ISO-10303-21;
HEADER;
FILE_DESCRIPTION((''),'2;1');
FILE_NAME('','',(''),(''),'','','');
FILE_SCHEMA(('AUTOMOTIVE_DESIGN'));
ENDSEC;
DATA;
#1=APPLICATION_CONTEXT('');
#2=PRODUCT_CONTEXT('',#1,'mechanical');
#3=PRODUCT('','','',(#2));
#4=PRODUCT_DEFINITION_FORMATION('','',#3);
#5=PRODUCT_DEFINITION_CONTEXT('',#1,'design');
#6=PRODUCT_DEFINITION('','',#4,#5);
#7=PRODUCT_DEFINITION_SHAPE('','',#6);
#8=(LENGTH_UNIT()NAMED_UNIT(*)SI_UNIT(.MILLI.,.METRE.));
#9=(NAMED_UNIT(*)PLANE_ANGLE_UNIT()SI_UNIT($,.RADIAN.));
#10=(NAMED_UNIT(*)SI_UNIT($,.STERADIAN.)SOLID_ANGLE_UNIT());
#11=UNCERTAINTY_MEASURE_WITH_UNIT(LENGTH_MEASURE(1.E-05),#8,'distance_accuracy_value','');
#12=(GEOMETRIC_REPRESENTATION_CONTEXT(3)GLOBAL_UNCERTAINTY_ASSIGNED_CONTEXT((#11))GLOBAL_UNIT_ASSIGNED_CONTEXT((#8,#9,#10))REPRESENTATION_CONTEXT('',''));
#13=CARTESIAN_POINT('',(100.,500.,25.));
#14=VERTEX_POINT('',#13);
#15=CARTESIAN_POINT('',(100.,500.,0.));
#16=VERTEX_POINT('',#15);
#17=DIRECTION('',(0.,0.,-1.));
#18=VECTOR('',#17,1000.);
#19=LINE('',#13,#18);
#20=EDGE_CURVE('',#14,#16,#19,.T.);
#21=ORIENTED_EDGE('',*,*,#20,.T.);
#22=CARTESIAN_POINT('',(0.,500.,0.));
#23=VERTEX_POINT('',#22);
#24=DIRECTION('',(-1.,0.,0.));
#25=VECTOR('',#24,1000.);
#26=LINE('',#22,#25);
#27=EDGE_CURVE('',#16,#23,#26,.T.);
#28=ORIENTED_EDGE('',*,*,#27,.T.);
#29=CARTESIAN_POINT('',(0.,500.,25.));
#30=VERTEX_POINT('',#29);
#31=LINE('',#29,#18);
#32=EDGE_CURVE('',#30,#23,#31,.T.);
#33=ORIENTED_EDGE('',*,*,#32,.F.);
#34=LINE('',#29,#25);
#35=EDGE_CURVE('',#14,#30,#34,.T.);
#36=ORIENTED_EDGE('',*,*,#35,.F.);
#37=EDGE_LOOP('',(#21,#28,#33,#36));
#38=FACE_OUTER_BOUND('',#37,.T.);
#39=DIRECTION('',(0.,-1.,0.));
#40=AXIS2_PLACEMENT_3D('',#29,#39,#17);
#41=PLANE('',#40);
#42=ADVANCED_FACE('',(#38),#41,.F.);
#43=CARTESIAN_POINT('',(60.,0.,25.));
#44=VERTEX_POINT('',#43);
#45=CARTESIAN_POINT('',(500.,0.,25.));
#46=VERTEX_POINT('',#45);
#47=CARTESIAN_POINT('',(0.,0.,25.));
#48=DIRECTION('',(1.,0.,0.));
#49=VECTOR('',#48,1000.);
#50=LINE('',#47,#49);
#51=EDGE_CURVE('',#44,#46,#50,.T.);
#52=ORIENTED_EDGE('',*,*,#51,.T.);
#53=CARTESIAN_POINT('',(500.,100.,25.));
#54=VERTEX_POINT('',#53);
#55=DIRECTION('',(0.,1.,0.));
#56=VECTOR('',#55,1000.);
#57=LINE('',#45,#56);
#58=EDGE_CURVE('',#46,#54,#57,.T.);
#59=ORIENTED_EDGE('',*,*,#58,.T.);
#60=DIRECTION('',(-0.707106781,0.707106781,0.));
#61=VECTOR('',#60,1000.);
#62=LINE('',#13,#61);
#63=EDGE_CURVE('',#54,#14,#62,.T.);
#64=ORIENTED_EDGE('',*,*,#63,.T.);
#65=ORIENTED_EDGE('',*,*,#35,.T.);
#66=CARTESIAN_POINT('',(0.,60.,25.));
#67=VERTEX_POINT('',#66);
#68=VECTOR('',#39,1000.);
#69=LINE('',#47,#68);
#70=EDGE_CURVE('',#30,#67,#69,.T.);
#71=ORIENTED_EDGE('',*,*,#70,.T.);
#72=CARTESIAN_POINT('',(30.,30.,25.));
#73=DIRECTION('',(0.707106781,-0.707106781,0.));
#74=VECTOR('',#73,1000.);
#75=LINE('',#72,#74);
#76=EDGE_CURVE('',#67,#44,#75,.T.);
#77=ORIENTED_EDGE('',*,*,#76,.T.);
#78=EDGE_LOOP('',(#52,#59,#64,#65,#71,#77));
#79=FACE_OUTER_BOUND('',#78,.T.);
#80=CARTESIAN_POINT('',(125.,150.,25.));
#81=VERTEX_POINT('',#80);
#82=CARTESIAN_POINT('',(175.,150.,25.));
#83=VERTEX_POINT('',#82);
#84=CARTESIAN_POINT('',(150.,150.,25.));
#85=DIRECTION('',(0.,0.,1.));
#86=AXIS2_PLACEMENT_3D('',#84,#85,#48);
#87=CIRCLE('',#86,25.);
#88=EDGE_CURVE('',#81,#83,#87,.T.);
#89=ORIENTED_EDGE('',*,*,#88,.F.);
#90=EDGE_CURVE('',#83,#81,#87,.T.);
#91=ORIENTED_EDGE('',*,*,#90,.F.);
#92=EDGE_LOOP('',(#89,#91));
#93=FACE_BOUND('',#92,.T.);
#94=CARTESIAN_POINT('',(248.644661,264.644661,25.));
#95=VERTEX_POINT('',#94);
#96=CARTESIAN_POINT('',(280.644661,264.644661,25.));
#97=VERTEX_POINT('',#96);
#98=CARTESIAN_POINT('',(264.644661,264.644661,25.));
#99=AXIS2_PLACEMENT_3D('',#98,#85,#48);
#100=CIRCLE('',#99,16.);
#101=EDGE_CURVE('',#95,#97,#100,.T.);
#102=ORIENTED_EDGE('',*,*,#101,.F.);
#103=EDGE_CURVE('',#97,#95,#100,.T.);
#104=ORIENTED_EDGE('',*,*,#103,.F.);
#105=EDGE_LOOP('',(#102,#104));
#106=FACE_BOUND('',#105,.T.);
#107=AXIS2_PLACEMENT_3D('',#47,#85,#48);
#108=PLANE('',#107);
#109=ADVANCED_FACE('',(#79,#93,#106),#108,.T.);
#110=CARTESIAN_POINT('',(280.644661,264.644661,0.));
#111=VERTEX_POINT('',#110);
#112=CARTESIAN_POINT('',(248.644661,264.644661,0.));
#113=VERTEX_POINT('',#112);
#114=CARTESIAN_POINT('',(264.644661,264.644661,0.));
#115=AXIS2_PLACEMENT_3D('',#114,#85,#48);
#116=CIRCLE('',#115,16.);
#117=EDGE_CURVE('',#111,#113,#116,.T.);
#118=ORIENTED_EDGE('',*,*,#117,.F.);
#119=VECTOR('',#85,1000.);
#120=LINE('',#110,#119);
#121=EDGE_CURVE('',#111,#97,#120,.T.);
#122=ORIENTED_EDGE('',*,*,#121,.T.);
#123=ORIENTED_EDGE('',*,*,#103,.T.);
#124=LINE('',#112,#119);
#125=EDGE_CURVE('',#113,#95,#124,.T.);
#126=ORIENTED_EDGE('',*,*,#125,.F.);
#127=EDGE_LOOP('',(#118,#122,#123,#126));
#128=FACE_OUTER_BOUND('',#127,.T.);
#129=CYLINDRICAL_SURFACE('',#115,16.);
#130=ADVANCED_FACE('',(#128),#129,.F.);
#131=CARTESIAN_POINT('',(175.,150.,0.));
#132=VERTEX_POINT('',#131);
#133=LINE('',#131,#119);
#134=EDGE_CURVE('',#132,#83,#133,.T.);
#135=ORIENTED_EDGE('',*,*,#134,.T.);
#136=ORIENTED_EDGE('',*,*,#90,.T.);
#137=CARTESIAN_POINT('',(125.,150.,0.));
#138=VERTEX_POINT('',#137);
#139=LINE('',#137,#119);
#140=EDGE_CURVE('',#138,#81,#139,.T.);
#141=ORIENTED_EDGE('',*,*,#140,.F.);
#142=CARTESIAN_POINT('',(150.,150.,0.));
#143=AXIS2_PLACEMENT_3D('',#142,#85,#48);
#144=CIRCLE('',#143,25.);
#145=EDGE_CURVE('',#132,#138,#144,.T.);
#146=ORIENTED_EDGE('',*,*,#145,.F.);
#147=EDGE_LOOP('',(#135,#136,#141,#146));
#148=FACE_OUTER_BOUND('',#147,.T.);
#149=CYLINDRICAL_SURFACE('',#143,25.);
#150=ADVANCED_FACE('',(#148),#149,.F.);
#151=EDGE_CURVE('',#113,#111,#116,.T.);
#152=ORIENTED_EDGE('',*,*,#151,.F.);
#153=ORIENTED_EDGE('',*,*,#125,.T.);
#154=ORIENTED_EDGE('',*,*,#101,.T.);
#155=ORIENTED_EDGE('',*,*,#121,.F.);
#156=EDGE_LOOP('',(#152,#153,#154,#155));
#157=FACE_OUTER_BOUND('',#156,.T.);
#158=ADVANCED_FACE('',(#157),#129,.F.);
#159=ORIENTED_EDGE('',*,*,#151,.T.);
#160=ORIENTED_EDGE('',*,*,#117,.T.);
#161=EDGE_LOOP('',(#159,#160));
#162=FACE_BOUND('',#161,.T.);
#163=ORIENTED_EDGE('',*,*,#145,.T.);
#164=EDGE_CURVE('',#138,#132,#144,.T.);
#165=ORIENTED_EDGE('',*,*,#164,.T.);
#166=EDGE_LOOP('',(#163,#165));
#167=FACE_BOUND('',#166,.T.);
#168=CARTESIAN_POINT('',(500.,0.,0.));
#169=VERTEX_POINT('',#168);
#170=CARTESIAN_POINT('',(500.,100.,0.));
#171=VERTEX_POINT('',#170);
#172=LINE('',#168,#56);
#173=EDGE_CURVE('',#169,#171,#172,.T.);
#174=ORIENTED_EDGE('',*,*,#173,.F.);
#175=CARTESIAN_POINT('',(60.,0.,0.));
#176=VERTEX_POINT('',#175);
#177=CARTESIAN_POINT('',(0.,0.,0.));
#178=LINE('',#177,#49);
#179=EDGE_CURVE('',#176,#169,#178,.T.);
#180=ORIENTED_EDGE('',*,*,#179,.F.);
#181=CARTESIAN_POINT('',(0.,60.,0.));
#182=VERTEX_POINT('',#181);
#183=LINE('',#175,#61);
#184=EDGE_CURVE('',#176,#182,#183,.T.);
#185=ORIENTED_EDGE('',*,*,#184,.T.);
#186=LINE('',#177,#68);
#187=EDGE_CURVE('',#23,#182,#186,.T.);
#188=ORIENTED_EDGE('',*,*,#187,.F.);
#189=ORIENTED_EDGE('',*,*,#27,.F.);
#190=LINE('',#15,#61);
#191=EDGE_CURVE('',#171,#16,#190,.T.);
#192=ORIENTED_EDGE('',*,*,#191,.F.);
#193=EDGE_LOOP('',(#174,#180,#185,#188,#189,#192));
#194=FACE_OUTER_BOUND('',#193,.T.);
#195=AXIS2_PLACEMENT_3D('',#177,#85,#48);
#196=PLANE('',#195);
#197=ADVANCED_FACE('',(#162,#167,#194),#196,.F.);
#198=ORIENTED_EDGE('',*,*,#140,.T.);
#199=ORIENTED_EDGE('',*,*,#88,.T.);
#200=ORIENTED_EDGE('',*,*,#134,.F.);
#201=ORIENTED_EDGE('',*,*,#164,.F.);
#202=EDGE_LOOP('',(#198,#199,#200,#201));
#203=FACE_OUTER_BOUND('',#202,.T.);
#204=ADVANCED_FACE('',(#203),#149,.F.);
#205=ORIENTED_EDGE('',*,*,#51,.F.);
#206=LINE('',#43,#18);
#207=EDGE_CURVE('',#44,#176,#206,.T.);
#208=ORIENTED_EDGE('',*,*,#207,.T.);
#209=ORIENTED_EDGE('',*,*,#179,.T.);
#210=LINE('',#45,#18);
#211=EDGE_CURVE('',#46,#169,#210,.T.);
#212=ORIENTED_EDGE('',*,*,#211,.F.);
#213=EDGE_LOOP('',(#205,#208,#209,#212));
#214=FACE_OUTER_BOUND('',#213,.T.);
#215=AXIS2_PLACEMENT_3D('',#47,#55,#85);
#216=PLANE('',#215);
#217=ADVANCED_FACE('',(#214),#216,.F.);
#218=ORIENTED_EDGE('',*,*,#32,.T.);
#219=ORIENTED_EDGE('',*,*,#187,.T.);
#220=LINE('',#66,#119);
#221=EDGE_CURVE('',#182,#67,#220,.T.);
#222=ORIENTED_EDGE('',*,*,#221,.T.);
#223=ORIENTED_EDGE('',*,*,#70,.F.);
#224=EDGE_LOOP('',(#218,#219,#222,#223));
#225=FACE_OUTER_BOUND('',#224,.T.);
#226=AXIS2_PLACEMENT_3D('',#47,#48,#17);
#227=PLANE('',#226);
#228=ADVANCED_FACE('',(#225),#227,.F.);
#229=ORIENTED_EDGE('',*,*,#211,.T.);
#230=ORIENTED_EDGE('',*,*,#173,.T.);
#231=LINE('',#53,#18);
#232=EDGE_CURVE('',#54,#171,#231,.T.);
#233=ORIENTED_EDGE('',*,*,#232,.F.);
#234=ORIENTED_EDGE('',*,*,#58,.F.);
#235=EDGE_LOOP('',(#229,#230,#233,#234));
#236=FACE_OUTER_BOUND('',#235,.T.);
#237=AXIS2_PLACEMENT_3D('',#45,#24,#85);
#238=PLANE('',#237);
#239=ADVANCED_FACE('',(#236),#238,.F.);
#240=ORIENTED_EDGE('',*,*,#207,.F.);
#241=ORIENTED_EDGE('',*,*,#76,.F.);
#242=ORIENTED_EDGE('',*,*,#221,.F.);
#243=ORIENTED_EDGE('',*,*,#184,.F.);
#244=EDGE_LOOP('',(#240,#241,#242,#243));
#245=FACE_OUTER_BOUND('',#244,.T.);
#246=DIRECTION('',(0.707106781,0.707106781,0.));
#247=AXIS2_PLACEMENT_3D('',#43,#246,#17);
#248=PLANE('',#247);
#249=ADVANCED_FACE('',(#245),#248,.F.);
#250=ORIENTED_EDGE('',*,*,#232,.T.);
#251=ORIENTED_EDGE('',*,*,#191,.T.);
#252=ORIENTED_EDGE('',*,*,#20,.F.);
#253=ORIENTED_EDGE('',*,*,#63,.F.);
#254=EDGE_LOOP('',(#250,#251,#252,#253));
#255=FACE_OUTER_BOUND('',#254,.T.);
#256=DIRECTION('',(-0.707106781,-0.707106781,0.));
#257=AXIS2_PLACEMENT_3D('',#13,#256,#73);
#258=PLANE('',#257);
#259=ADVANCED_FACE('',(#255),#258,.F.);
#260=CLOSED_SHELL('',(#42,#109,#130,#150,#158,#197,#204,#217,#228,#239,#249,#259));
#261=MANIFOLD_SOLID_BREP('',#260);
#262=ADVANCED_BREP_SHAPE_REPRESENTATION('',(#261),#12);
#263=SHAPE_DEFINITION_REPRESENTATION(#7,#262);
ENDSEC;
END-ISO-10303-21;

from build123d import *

# Parameters (mm, degrees)
BOSS_EXTRUDE1_DEPTH = 25
SKETCH2_R           = 25
CUT_EXTRUDE1_DEPTH  = 25
CHAMFER1_SIZE       = 60
SKETCH3_R           = 16
CUT_EXTRUDE2_DEPTH  = 708.548584904


with BuildPart() as part:
    # Sketch1 → Boss-Extrude1 (new body)
    with BuildSketch(Plane.XY):
        Polygon((0, 0), (0, 500), (100, 500), (500, 100), (500, 0), align=None)
    extrude(amount=BOSS_EXTRUDE1_DEPTH)

    # Sketch2 → Cut-Extrude1 (cut)
    with BuildSketch(Plane.XY.offset(25)):
        with Locations((150, 150)):
            Circle(SKETCH2_R)
    extrude(amount=-CUT_EXTRUDE1_DEPTH, mode=Mode.SUBTRACT)

    # Chamfer1
    chamfer1_edges = [part.edges().sort_by_distance(p)[0] for p in [
        (0, 0, 12.5),
    ]]
    chamfer(chamfer1_edges, length=CHAMFER1_SIZE)

    # Sketch3 → Cut-Extrude2 (cut, through all)
    with BuildSketch(Plane.XY.offset(25)):
        with Locations((264.644660941, 264.644660941)):
            Circle(SKETCH3_R)
    extrude(amount=-CUT_EXTRUDE2_DEPTH, mode=Mode.SUBTRACT)


solid = part.part
